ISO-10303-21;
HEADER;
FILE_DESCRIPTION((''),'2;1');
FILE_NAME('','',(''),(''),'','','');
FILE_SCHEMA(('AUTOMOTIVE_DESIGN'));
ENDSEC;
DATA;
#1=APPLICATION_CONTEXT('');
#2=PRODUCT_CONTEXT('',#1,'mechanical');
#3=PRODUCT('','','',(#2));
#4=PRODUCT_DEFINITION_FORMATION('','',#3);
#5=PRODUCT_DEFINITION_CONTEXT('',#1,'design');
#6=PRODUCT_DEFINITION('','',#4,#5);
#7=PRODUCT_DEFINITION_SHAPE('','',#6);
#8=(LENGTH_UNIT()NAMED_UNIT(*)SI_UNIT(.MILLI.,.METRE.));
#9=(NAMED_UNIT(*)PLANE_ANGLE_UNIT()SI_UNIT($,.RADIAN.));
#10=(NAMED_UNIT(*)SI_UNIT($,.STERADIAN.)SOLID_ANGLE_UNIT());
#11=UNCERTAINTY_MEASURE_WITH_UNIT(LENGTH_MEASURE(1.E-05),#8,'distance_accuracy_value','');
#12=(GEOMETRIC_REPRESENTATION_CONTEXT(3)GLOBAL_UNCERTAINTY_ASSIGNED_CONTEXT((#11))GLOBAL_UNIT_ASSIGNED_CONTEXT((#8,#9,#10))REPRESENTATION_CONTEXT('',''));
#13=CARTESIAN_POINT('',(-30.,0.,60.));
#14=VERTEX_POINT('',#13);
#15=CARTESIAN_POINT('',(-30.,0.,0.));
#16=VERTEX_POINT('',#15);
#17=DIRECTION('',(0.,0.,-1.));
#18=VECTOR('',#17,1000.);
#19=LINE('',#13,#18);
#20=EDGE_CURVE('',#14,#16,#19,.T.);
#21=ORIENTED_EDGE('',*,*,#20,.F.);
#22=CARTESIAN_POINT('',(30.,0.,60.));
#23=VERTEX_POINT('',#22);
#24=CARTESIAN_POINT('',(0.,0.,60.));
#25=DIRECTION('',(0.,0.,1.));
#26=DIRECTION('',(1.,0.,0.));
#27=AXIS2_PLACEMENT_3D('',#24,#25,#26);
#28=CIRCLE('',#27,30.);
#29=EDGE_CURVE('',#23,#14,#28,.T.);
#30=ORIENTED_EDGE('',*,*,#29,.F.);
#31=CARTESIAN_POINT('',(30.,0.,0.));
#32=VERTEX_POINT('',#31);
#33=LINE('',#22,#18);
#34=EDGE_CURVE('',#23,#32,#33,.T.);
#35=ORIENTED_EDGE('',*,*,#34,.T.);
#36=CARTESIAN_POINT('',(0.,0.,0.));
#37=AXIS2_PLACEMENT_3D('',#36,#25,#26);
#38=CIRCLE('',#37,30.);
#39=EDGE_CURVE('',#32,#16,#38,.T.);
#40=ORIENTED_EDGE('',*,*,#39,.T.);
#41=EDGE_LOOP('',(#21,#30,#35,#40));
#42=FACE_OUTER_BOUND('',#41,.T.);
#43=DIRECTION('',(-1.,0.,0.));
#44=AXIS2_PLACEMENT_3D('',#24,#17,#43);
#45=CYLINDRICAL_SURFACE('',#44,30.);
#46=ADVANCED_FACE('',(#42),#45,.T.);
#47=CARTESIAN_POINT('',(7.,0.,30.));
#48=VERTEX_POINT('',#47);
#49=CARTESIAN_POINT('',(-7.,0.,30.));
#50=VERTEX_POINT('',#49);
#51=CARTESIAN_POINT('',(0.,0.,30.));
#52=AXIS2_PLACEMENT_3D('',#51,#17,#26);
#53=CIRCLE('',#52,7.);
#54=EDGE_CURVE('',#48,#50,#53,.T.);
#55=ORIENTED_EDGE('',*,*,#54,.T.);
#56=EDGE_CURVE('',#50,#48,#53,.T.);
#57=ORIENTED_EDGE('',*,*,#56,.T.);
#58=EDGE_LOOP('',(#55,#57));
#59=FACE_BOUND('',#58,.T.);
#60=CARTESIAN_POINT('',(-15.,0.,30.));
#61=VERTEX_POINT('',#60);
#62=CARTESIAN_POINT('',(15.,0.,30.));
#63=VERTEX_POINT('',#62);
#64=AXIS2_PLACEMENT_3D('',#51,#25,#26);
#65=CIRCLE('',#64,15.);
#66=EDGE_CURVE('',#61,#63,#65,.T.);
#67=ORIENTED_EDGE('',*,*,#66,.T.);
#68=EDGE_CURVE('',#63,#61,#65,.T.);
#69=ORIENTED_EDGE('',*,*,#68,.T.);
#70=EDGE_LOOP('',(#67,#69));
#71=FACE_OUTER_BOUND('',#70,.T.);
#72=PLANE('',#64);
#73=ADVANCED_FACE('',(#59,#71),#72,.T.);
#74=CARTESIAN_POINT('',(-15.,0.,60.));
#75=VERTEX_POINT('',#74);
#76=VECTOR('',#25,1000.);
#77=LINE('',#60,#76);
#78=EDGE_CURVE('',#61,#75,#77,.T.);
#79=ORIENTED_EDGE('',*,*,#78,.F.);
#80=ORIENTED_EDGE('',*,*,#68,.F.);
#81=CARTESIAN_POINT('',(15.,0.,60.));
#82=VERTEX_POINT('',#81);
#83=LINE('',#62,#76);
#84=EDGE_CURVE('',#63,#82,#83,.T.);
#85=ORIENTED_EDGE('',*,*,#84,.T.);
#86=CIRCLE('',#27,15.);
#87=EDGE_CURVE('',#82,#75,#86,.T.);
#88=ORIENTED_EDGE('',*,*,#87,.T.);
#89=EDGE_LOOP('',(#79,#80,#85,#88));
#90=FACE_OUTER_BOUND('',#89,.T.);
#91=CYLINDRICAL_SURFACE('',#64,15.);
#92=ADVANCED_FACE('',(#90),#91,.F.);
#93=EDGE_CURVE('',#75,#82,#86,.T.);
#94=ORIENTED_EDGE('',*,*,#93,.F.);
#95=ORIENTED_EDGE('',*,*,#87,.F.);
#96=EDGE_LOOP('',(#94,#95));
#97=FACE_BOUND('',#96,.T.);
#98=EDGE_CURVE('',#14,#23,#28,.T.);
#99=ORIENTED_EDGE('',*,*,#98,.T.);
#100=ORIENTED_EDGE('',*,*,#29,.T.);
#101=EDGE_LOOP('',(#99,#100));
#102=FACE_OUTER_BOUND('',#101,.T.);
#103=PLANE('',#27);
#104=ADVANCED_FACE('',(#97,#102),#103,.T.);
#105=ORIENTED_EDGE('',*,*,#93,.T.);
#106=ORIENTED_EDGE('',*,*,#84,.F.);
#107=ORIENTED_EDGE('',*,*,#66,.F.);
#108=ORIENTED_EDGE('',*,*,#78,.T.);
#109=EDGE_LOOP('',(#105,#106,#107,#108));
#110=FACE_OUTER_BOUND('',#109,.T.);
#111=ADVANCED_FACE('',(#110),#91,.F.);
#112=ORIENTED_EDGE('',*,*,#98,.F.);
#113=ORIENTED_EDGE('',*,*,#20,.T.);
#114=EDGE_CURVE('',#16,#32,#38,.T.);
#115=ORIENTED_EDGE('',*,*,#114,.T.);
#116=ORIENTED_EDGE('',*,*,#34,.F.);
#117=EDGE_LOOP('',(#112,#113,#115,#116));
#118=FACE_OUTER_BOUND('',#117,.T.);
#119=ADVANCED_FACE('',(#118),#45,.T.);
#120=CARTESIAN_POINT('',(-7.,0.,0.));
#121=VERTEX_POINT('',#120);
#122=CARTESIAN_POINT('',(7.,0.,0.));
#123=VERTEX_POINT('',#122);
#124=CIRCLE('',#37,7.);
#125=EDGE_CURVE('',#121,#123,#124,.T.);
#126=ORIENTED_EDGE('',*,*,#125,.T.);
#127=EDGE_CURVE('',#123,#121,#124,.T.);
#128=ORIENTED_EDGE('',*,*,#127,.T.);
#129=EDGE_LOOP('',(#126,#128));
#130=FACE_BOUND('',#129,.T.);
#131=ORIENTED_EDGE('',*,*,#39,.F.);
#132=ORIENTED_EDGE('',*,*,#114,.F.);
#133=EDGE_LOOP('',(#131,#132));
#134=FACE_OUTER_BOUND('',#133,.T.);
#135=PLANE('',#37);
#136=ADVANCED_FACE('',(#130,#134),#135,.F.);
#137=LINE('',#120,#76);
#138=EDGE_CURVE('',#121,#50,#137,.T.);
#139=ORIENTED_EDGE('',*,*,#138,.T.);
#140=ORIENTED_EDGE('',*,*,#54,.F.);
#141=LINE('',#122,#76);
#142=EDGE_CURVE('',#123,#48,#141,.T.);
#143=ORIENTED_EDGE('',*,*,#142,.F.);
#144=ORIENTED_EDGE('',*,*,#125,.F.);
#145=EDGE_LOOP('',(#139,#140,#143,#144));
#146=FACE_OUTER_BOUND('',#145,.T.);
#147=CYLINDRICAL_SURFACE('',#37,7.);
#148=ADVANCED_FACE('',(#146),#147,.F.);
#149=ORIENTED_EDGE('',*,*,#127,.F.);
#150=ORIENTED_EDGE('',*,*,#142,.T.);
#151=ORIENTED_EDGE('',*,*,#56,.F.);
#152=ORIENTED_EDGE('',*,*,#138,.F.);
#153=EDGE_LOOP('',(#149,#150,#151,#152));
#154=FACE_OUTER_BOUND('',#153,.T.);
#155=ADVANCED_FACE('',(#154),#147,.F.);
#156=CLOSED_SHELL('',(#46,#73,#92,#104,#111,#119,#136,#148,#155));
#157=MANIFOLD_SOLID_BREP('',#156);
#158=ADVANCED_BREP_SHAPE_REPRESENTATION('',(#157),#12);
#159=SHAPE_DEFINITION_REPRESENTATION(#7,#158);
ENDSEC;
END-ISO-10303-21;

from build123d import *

# Parameters (mm, degrees)
SKETCH_1_R          = 30
EXTRUDE_1_DEPTH     = 60
SKETCH_2_R          = 7
CUT_EXTRUDE_1_DEPTH = 74.484692283
SKETCH_3_R          = 15
CUT_EXTRUDE_2_DEPTH = 30


with BuildPart() as part:
    # 草图1 → 凸台-拉伸1 (new body)
    with BuildSketch(Plane.XY):
        Circle(SKETCH_1_R)
    extrude(amount=EXTRUDE_1_DEPTH)

    # 草图2 → 切除-拉伸1 (cut, through all)
    with BuildSketch(Plane.XY.offset(60)):
        Circle(SKETCH_2_R)
    extrude(amount=-CUT_EXTRUDE_1_DEPTH, mode=Mode.SUBTRACT)

    # 草图3 → 切除-拉伸2 (cut)
    with BuildSketch(Plane.XY.offset(60)):
        Circle(SKETCH_3_R)
    extrude(amount=-CUT_EXTRUDE_2_DEPTH, mode=Mode.SUBTRACT)


solid = part.part
